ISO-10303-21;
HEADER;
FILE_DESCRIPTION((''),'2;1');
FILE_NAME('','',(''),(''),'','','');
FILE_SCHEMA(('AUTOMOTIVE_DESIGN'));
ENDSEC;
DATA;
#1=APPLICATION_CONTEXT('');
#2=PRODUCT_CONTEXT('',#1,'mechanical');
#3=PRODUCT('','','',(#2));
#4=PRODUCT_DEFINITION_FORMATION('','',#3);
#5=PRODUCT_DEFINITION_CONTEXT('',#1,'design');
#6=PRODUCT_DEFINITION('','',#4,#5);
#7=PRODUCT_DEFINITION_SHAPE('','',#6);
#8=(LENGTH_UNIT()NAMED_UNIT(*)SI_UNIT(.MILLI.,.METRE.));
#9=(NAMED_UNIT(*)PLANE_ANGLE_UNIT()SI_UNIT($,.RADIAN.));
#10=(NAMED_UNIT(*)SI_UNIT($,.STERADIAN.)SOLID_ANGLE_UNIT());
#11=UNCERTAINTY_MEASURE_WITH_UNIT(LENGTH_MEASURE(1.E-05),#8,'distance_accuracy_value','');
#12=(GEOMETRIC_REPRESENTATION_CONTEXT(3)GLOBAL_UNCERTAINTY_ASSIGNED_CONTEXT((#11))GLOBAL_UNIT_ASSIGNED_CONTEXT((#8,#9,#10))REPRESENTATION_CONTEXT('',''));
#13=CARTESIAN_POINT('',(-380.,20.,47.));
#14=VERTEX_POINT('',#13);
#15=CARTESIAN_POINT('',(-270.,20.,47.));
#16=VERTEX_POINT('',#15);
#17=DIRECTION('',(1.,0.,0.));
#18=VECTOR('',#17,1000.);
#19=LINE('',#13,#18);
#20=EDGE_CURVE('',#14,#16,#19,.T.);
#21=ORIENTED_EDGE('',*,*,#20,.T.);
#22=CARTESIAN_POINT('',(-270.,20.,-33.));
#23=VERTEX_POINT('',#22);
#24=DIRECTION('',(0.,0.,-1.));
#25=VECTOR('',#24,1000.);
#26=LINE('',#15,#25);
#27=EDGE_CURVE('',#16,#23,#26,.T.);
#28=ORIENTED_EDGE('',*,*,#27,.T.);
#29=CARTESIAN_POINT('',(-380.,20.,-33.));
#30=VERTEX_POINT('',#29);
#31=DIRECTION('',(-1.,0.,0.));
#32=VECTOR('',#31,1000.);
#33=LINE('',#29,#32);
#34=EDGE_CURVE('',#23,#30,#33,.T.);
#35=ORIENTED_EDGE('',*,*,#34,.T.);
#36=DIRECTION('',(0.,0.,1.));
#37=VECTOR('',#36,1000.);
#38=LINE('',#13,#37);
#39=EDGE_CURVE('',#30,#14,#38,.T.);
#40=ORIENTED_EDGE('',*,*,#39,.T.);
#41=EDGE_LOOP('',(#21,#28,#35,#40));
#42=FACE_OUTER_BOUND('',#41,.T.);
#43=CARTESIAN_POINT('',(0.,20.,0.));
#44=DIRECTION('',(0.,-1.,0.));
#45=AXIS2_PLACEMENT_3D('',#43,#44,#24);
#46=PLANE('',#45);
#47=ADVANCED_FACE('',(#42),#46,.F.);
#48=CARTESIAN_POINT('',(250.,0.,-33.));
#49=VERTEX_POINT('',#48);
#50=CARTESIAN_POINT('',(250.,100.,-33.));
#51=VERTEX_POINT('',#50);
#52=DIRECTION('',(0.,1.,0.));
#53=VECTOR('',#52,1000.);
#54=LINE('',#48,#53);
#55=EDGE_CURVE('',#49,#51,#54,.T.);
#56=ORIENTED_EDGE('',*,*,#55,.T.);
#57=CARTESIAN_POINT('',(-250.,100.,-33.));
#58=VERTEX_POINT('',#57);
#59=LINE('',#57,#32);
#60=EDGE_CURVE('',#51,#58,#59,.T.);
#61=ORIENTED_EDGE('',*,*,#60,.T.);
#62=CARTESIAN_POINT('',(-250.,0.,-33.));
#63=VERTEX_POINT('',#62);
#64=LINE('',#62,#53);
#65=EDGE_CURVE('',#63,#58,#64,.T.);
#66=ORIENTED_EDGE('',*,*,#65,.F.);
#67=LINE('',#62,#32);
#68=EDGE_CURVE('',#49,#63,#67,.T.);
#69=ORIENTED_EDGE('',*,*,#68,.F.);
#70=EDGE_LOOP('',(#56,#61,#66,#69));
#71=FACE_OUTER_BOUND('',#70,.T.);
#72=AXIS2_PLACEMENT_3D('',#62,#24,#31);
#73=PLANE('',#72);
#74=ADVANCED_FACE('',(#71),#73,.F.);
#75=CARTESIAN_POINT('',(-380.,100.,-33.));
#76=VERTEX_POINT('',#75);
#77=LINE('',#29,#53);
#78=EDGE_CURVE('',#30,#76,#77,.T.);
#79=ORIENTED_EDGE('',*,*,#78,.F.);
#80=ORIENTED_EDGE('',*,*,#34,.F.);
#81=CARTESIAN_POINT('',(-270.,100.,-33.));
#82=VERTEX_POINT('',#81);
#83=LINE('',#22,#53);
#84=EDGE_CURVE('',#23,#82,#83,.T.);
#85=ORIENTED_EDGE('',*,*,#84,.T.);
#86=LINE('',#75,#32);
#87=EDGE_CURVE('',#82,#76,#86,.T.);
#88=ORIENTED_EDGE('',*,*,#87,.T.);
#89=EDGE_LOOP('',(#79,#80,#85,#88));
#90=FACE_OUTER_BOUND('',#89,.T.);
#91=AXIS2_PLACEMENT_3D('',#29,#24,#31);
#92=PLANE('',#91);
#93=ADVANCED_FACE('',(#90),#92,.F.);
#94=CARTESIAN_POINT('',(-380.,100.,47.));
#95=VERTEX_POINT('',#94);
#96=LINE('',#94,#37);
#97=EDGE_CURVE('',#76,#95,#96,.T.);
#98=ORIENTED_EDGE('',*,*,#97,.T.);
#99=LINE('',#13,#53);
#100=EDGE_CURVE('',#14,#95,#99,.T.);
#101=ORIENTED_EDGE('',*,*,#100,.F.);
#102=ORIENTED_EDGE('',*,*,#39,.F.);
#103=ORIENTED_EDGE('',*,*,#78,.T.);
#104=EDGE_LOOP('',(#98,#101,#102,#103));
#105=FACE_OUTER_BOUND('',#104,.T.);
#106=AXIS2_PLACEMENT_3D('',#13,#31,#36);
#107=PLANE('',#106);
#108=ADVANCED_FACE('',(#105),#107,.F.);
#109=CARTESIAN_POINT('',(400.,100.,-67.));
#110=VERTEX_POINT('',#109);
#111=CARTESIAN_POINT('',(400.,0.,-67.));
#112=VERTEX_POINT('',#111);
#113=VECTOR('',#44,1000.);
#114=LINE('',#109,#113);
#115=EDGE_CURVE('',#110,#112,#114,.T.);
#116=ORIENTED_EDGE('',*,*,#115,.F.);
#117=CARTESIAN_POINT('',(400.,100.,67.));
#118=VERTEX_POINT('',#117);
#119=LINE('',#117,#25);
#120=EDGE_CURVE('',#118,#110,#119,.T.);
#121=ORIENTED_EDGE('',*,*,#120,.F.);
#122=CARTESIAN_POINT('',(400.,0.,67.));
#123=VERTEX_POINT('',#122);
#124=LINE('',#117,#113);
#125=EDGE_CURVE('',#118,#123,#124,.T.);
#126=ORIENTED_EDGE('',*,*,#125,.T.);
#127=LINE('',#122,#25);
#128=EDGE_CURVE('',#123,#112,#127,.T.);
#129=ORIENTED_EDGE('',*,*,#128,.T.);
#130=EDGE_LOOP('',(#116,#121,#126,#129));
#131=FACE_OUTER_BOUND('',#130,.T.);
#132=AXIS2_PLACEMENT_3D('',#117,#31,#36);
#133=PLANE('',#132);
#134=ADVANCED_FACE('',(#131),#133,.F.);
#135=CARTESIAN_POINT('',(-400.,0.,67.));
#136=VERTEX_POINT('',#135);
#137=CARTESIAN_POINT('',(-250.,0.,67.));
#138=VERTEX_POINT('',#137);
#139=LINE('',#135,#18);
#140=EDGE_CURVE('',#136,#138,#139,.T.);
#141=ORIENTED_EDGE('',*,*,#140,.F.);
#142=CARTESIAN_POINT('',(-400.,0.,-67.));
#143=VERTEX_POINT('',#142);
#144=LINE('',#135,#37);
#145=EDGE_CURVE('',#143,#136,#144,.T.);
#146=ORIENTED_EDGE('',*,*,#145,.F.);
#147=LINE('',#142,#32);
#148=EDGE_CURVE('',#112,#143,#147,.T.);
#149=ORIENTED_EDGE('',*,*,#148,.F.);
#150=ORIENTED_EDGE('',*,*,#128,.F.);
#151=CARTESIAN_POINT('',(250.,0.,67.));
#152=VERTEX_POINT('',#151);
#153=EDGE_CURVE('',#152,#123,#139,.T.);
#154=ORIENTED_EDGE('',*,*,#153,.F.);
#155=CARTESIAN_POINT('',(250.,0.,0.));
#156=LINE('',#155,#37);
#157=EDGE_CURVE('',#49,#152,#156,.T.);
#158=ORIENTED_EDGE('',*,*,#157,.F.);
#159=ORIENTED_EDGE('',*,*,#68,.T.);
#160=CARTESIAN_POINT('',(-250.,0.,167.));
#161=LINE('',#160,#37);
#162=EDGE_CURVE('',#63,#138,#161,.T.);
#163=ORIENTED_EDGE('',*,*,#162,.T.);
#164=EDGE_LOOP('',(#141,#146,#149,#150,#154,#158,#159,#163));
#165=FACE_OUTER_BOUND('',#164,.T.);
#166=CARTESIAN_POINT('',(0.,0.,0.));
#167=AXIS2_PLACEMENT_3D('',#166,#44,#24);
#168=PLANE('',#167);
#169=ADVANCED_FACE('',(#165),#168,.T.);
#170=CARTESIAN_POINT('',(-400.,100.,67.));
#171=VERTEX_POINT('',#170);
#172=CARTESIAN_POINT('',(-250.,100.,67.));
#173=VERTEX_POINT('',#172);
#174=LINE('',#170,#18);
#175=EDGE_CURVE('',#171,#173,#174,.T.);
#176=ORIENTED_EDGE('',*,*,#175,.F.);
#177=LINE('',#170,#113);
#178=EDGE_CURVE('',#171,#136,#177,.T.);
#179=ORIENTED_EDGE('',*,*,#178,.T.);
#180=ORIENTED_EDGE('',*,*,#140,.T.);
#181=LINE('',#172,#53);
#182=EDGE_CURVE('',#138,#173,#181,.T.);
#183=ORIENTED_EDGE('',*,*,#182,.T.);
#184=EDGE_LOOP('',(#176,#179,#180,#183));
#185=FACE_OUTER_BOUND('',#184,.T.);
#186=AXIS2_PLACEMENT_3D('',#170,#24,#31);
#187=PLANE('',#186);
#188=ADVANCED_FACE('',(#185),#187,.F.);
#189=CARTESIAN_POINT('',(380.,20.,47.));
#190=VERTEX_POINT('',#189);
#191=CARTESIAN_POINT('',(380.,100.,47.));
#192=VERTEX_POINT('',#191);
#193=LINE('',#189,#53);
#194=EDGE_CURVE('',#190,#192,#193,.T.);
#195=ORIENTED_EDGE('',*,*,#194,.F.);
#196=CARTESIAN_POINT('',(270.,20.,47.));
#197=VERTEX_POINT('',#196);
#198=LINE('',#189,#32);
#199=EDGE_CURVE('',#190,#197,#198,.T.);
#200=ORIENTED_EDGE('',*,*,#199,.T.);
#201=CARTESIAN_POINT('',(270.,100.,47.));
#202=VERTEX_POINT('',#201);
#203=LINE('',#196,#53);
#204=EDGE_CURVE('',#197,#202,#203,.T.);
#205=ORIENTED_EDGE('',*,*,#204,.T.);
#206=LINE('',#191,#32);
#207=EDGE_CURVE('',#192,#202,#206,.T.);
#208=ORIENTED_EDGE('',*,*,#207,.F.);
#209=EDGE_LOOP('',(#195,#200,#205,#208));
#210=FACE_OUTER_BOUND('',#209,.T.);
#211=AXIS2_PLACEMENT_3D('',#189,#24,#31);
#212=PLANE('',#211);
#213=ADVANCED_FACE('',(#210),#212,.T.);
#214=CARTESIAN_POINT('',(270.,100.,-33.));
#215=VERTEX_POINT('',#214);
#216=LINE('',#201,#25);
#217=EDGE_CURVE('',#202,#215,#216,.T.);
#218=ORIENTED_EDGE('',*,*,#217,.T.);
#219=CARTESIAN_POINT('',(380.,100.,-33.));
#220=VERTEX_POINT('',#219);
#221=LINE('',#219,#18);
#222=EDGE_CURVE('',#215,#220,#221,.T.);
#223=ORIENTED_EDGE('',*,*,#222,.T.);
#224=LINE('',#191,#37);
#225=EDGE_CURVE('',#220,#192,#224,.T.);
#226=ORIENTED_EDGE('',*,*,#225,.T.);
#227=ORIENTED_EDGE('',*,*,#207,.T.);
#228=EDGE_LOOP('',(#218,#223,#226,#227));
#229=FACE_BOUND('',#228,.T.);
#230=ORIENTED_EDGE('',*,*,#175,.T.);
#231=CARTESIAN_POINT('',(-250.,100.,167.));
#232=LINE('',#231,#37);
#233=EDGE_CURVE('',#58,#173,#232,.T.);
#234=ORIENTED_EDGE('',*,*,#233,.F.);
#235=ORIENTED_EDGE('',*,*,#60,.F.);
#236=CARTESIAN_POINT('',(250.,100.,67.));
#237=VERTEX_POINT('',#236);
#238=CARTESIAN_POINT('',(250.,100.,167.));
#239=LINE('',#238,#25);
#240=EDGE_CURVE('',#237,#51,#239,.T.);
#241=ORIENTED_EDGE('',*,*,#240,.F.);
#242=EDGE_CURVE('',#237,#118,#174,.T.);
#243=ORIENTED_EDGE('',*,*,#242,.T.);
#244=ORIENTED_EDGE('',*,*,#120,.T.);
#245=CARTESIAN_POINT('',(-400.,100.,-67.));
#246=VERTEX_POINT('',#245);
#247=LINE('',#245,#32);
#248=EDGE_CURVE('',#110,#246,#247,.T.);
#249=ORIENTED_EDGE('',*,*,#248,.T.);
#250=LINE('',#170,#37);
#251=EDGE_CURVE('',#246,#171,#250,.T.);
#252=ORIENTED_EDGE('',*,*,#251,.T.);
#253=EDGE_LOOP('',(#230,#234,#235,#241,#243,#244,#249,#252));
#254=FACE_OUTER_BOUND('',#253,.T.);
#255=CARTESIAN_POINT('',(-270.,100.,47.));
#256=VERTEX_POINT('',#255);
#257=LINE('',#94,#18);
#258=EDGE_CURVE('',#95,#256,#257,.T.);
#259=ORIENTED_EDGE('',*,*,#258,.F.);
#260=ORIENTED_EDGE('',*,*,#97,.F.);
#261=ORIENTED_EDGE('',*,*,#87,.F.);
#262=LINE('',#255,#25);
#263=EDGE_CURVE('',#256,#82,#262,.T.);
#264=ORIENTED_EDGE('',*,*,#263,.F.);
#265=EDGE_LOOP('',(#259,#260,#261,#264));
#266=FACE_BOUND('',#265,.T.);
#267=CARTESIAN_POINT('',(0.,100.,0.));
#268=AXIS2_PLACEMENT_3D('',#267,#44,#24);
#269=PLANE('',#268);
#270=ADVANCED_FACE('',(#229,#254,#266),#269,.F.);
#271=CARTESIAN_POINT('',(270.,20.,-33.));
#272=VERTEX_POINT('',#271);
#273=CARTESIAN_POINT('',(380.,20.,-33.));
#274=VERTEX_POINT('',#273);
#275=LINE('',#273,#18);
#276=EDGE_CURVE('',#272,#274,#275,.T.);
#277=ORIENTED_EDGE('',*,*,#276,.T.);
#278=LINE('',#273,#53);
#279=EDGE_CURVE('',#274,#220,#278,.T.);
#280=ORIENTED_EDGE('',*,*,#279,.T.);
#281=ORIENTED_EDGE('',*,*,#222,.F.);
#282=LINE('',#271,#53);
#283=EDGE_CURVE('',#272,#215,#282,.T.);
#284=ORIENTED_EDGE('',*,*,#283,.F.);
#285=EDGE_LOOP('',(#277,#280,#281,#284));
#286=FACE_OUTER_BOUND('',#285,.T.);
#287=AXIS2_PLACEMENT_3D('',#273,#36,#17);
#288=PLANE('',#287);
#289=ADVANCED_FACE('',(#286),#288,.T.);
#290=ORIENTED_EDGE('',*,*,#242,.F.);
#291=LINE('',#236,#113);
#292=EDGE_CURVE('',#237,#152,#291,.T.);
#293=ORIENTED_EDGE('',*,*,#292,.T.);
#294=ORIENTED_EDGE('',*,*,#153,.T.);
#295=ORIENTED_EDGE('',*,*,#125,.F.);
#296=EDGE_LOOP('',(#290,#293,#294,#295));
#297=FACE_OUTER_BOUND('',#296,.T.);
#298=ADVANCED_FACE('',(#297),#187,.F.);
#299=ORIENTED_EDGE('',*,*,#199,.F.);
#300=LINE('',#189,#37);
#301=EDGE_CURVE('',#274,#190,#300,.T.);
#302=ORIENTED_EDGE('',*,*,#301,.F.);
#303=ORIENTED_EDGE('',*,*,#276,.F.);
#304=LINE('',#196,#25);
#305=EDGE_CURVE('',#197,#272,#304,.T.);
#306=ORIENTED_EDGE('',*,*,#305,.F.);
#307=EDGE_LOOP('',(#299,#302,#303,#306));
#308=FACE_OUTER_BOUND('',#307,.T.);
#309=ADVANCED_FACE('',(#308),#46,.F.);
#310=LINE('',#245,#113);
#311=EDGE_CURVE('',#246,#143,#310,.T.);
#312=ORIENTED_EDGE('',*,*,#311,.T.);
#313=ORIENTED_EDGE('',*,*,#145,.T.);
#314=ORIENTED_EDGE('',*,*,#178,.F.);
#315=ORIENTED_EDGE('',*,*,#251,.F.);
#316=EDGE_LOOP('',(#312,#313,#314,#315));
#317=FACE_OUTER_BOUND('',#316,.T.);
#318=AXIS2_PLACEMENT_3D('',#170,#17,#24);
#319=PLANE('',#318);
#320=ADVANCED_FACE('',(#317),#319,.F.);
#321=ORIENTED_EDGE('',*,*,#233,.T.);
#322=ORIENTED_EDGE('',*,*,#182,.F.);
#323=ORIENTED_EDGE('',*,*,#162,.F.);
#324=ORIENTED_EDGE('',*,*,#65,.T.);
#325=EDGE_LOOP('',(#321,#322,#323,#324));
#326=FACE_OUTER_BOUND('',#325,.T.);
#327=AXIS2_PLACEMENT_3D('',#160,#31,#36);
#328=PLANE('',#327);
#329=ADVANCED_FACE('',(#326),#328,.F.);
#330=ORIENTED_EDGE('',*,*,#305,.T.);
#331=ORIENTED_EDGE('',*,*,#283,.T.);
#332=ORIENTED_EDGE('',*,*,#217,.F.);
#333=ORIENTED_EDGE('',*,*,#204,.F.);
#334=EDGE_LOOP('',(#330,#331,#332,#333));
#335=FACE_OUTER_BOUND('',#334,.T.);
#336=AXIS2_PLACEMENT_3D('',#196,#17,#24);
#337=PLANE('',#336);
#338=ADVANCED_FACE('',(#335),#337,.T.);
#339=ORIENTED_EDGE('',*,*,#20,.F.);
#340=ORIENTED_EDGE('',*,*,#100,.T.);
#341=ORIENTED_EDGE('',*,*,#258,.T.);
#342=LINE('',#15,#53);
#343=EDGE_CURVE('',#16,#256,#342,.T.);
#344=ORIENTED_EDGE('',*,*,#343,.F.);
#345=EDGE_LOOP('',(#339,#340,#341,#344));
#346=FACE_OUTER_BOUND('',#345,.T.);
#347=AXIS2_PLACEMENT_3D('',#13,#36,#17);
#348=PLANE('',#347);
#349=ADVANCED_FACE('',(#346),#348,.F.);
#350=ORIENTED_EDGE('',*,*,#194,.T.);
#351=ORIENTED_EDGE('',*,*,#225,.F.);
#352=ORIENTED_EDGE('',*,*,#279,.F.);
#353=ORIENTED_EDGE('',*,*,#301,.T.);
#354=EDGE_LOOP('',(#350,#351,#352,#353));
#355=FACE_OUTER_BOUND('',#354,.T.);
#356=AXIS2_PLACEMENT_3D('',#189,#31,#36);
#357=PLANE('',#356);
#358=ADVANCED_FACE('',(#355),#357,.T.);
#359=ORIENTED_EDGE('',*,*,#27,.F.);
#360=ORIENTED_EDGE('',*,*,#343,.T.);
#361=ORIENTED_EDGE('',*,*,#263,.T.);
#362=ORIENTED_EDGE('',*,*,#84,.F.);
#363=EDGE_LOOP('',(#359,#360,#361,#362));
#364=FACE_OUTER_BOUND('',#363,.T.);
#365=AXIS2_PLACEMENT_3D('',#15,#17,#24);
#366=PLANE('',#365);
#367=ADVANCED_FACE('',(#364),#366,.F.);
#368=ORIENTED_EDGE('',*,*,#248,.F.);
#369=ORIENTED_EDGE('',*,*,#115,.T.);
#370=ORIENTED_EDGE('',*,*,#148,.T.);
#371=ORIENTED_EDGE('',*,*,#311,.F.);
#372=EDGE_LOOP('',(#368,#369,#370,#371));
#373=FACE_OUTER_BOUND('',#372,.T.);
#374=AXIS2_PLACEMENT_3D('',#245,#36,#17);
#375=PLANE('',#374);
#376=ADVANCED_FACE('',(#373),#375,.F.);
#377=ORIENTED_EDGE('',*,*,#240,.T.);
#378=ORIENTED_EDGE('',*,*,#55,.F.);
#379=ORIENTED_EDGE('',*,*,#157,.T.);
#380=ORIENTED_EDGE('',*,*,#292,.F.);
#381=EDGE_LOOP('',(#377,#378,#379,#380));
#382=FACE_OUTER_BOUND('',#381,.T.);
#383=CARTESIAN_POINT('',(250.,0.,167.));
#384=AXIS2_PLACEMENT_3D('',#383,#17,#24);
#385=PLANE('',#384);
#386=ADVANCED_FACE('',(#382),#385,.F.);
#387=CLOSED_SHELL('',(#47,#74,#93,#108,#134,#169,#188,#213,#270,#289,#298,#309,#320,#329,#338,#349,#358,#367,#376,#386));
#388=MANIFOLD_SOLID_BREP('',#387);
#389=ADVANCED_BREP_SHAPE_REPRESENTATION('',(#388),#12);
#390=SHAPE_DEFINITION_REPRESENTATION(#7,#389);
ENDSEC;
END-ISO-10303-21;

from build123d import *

# Parameters (mm, degrees)
SKETCH1_W           = 800
SKETCH1_H           = 134
BOSS_EXTRUDE1_DEPTH = 100
SKETCH2_W           = 500
SKETCH2_H           = 200
CUT_EXTRUDE1_DEPTH  = 100
SKETCH3_W           = 110
SKETCH3_H           = 80
CUT_EXTRUDE2_DEPTH  = 80


with BuildPart() as part:
    # Sketch1 → Boss-Extrude1 (new body)
    with BuildSketch(Plane(origin=(0, 0, 0), x_dir=(1, 0, 0), z_dir=(0, 1, 0))):
        Rectangle(SKETCH1_W, SKETCH1_H)
    extrude(amount=BOSS_EXTRUDE1_DEPTH)

    # Sketch2 → Cut-Extrude1 (cut)
    with BuildSketch(Plane(origin=(0, 100, 0), x_dir=(1, 0, 0), z_dir=(0, 1, 0))):
        with Locations((0, -67)):
            Rectangle(SKETCH2_W, SKETCH2_H)
    extrude(amount=-CUT_EXTRUDE1_DEPTH, mode=Mode.SUBTRACT)

    # Sketch3 → Cut-Extrude2 (cut)
    with BuildSketch(Plane(origin=(0, 100, 0), x_dir=(1, 0, 0), z_dir=(0, 1, 0))):
        with Locations((-325, -7)):
            Rectangle(SKETCH3_W, SKETCH3_H)
    cut_extrude2 = extrude(amount=-CUT_EXTRUDE2_DEPTH, mode=Mode.SUBTRACT)

    # Mirror1: Cut-Extrude2 across plane
    add(cut_extrude2.mirror(Plane(origin=(0, 0, 0), x_dir=(0, 0, 1), z_dir=(1, 0, 0))), mode=Mode.SUBTRACT)


solid = part.part
